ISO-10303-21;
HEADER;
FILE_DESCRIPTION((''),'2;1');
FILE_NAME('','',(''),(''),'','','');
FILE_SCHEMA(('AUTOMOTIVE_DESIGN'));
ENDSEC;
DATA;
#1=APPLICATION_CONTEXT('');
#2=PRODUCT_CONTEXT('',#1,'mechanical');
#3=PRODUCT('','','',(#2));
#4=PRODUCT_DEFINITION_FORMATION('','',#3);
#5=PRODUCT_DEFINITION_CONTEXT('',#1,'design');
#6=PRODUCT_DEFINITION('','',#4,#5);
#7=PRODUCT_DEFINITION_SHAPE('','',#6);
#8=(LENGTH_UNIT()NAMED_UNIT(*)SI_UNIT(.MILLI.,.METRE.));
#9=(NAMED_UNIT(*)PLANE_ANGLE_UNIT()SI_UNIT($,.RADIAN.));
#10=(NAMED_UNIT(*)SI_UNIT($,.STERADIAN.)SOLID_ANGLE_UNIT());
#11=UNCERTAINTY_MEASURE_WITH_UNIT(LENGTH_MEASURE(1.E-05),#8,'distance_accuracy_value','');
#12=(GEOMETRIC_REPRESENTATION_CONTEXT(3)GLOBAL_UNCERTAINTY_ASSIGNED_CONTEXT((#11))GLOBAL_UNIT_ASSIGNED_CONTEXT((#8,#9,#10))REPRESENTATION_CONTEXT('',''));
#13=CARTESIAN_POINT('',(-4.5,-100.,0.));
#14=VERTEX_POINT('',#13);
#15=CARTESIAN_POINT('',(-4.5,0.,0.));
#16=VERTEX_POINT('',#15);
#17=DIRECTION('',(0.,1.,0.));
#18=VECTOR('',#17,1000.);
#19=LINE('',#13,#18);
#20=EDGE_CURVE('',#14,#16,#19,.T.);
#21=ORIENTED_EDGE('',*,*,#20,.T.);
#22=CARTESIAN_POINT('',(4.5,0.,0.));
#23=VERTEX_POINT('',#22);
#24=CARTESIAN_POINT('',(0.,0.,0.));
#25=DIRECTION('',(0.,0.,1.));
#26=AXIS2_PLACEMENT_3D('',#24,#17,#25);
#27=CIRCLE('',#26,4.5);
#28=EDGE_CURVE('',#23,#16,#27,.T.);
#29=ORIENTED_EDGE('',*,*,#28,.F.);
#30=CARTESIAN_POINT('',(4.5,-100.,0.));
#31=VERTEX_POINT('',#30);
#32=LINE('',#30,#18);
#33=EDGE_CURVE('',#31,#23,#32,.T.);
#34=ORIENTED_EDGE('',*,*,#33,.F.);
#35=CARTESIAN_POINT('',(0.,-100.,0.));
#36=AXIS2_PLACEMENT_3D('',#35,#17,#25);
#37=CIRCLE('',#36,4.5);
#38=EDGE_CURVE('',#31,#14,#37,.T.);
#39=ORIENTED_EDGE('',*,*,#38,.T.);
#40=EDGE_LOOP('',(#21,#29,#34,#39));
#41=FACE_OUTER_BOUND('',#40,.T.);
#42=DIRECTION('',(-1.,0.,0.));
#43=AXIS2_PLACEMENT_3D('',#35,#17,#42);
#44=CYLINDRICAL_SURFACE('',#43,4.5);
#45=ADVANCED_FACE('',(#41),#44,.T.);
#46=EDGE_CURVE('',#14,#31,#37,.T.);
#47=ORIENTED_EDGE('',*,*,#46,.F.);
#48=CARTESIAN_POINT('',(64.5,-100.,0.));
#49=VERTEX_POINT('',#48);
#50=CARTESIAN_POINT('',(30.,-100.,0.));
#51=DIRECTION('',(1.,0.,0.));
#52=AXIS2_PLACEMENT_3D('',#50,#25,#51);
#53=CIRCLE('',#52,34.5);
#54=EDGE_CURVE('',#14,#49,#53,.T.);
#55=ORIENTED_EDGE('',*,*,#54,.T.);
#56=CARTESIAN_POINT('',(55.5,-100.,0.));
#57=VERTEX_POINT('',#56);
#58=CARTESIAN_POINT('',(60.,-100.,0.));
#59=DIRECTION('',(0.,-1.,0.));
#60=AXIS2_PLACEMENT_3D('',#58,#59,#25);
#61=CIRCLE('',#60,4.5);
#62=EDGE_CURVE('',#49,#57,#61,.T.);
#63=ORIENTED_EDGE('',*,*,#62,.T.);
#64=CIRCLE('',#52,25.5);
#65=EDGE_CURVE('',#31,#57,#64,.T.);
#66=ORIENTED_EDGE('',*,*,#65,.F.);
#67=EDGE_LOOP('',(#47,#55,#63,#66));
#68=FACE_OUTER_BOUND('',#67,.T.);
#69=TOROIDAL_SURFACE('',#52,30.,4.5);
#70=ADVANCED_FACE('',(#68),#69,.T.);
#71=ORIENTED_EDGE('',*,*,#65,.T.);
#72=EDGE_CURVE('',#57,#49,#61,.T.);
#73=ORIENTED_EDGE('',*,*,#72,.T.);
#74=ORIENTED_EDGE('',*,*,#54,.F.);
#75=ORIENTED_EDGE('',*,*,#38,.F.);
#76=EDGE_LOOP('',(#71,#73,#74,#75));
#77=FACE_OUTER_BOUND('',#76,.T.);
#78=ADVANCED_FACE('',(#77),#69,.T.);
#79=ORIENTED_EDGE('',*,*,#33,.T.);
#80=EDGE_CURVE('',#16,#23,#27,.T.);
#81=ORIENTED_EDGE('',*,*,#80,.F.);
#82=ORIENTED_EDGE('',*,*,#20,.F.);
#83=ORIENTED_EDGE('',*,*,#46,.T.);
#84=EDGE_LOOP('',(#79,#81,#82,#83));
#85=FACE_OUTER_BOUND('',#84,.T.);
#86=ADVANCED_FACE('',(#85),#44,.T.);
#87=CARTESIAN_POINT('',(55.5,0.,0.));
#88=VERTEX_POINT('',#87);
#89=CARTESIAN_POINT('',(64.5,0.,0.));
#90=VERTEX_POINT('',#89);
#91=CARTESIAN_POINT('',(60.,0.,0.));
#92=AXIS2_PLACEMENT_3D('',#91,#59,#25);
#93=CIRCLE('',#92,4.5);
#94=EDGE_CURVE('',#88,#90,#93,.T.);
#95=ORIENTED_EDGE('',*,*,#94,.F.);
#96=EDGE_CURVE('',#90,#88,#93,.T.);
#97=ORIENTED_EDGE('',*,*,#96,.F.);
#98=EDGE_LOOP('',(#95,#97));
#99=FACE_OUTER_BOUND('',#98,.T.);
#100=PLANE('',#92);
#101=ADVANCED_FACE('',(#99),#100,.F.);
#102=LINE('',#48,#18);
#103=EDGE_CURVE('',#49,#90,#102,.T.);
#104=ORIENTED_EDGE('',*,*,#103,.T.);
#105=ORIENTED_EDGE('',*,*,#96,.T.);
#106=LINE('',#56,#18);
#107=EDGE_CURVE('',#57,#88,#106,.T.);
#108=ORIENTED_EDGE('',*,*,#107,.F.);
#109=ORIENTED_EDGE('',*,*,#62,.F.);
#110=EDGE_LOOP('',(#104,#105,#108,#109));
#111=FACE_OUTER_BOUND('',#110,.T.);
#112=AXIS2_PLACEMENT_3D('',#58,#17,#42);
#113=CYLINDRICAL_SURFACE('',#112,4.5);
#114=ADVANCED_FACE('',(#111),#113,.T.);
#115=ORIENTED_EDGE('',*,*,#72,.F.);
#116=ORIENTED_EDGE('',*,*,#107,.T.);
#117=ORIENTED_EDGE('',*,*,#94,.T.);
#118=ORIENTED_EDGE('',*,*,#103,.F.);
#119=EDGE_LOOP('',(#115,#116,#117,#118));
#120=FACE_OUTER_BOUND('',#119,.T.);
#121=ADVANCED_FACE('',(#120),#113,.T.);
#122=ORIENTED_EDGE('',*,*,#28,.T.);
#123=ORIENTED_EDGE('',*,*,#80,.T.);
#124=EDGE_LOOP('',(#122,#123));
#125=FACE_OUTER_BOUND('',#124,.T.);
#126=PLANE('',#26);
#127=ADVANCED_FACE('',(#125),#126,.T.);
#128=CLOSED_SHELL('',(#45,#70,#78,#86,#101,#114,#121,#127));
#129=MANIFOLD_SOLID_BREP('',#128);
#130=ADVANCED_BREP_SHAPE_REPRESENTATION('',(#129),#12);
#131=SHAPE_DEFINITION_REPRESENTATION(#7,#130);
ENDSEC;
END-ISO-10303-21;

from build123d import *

# Parameters (mm, degrees)
SKETCH2_R = 4.5


with BuildPart() as part:
    # Sweep1: sweep along a path in Sketch1
    with BuildLine(Plane.XY) as sweep1_path:
        Line((60, 0), (60, -100))
        ThreePointArc((60, -100), (30, -130), (0, -100))
        Line((0, -100), (0, 0))
    # Sketch2 → Sweep1 (sweep)
    with BuildSketch(Plane(origin=(0, 0, 0), x_dir=(1, 0, 0), z_dir=(0, 1, 0))):
        Circle(SKETCH2_R)
    sweep(path=sweep1_path.line)


solid = part.part
